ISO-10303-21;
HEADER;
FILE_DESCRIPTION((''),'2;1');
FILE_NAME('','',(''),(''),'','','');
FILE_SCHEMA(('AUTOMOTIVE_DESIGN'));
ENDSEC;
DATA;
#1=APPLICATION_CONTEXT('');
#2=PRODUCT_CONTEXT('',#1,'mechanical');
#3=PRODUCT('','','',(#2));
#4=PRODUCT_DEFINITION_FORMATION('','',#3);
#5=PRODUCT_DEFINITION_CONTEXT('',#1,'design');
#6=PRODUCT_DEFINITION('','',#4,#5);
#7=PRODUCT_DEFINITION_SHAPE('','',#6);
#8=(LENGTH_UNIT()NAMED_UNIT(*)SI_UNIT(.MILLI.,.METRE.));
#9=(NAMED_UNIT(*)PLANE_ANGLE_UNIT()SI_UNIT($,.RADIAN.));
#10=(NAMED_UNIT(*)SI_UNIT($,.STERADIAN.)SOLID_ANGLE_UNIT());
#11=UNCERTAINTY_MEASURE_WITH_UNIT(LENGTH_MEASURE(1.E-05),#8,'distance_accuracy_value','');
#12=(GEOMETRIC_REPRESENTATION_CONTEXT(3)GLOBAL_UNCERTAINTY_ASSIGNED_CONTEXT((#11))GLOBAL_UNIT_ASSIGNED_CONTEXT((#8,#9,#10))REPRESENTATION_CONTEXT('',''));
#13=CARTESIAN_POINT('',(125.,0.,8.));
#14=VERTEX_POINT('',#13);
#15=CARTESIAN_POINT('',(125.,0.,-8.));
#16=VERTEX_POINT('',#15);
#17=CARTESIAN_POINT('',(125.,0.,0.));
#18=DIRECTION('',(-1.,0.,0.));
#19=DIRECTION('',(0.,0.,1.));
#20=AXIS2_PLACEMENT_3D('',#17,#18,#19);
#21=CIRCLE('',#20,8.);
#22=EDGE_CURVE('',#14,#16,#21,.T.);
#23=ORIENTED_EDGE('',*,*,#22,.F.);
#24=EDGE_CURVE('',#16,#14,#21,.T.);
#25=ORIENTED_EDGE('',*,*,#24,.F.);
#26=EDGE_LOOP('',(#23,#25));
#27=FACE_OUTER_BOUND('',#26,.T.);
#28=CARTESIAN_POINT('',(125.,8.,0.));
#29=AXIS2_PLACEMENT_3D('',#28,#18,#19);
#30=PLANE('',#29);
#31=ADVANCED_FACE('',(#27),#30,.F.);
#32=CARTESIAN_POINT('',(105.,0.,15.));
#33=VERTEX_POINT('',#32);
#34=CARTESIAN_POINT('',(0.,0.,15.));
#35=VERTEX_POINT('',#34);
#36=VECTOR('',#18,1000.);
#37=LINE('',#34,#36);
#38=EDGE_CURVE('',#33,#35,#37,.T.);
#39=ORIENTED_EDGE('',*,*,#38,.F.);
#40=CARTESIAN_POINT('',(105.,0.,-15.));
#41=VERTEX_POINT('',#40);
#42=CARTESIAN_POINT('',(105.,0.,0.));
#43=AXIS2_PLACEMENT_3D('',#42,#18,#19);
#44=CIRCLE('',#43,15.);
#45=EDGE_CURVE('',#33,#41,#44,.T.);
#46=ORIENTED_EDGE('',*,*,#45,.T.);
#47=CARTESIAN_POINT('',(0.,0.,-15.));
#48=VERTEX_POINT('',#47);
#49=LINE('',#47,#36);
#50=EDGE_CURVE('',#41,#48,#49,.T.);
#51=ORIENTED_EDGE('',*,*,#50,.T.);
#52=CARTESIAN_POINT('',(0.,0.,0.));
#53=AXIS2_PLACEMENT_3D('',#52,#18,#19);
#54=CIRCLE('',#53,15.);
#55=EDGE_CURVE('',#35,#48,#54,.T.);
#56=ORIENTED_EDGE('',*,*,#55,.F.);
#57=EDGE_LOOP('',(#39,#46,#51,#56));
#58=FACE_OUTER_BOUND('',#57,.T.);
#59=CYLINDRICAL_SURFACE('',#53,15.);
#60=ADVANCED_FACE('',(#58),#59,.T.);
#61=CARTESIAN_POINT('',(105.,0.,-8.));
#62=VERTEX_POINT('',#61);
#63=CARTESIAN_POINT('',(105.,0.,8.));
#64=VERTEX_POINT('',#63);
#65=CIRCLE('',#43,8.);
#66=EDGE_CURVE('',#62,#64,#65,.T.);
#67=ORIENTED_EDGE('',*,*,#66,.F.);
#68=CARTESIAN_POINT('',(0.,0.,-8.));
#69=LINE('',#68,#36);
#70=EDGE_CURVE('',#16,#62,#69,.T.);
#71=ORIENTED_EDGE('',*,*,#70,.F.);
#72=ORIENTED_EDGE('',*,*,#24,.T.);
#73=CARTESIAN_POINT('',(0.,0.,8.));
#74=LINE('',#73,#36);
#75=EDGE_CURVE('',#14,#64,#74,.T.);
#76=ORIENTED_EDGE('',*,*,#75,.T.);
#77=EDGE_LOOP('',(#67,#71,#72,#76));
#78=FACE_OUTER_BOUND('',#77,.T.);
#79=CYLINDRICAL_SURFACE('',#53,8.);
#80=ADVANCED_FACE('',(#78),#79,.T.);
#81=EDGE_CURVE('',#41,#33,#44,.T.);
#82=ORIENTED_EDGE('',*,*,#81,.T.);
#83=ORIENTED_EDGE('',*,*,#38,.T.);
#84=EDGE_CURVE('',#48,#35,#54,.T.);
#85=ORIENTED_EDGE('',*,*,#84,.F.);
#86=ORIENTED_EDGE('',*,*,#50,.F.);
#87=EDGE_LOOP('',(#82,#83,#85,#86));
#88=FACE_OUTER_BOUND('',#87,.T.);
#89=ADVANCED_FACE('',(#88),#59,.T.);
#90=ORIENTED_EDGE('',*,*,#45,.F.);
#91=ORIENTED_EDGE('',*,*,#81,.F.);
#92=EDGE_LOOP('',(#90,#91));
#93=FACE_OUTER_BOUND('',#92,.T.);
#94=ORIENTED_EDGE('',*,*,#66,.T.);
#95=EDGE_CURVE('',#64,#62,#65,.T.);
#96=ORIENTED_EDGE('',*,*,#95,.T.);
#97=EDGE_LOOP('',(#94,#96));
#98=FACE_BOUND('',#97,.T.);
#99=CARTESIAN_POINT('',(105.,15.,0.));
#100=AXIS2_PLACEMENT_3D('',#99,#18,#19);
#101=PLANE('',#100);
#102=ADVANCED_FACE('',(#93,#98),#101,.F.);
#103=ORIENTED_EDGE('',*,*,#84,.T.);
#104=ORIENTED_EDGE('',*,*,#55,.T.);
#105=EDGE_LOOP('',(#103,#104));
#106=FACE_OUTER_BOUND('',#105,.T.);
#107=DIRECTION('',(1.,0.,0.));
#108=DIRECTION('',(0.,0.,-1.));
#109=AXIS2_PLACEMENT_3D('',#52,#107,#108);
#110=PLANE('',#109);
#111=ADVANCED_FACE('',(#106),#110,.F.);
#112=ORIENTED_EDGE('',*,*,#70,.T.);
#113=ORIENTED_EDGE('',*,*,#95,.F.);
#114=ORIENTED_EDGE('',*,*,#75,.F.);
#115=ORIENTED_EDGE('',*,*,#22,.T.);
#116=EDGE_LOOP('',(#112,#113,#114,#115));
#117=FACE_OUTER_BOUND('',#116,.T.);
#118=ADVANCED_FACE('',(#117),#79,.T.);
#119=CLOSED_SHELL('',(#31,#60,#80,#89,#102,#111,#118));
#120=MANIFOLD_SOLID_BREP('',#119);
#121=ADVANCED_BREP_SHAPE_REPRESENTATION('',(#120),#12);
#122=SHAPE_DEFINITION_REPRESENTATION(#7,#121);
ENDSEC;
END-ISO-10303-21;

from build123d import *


with BuildPart() as part:
    # Sketch1 → Revolve1 (revolve)
    with BuildSketch(Plane.XY, mode=Mode.PRIVATE) as revolve1_sk:
        Polygon((0, 0), (0, 15), (105, 15), (105, 8), (125, 8), (125, 0), align=None)
    revolve(revolve1_sk.sketch.rotate(Axis((0, 0, 0), (1, 0, 0)), 90), axis=Axis((0, 0, 0), (1, 0, 0)))


solid = part.part
